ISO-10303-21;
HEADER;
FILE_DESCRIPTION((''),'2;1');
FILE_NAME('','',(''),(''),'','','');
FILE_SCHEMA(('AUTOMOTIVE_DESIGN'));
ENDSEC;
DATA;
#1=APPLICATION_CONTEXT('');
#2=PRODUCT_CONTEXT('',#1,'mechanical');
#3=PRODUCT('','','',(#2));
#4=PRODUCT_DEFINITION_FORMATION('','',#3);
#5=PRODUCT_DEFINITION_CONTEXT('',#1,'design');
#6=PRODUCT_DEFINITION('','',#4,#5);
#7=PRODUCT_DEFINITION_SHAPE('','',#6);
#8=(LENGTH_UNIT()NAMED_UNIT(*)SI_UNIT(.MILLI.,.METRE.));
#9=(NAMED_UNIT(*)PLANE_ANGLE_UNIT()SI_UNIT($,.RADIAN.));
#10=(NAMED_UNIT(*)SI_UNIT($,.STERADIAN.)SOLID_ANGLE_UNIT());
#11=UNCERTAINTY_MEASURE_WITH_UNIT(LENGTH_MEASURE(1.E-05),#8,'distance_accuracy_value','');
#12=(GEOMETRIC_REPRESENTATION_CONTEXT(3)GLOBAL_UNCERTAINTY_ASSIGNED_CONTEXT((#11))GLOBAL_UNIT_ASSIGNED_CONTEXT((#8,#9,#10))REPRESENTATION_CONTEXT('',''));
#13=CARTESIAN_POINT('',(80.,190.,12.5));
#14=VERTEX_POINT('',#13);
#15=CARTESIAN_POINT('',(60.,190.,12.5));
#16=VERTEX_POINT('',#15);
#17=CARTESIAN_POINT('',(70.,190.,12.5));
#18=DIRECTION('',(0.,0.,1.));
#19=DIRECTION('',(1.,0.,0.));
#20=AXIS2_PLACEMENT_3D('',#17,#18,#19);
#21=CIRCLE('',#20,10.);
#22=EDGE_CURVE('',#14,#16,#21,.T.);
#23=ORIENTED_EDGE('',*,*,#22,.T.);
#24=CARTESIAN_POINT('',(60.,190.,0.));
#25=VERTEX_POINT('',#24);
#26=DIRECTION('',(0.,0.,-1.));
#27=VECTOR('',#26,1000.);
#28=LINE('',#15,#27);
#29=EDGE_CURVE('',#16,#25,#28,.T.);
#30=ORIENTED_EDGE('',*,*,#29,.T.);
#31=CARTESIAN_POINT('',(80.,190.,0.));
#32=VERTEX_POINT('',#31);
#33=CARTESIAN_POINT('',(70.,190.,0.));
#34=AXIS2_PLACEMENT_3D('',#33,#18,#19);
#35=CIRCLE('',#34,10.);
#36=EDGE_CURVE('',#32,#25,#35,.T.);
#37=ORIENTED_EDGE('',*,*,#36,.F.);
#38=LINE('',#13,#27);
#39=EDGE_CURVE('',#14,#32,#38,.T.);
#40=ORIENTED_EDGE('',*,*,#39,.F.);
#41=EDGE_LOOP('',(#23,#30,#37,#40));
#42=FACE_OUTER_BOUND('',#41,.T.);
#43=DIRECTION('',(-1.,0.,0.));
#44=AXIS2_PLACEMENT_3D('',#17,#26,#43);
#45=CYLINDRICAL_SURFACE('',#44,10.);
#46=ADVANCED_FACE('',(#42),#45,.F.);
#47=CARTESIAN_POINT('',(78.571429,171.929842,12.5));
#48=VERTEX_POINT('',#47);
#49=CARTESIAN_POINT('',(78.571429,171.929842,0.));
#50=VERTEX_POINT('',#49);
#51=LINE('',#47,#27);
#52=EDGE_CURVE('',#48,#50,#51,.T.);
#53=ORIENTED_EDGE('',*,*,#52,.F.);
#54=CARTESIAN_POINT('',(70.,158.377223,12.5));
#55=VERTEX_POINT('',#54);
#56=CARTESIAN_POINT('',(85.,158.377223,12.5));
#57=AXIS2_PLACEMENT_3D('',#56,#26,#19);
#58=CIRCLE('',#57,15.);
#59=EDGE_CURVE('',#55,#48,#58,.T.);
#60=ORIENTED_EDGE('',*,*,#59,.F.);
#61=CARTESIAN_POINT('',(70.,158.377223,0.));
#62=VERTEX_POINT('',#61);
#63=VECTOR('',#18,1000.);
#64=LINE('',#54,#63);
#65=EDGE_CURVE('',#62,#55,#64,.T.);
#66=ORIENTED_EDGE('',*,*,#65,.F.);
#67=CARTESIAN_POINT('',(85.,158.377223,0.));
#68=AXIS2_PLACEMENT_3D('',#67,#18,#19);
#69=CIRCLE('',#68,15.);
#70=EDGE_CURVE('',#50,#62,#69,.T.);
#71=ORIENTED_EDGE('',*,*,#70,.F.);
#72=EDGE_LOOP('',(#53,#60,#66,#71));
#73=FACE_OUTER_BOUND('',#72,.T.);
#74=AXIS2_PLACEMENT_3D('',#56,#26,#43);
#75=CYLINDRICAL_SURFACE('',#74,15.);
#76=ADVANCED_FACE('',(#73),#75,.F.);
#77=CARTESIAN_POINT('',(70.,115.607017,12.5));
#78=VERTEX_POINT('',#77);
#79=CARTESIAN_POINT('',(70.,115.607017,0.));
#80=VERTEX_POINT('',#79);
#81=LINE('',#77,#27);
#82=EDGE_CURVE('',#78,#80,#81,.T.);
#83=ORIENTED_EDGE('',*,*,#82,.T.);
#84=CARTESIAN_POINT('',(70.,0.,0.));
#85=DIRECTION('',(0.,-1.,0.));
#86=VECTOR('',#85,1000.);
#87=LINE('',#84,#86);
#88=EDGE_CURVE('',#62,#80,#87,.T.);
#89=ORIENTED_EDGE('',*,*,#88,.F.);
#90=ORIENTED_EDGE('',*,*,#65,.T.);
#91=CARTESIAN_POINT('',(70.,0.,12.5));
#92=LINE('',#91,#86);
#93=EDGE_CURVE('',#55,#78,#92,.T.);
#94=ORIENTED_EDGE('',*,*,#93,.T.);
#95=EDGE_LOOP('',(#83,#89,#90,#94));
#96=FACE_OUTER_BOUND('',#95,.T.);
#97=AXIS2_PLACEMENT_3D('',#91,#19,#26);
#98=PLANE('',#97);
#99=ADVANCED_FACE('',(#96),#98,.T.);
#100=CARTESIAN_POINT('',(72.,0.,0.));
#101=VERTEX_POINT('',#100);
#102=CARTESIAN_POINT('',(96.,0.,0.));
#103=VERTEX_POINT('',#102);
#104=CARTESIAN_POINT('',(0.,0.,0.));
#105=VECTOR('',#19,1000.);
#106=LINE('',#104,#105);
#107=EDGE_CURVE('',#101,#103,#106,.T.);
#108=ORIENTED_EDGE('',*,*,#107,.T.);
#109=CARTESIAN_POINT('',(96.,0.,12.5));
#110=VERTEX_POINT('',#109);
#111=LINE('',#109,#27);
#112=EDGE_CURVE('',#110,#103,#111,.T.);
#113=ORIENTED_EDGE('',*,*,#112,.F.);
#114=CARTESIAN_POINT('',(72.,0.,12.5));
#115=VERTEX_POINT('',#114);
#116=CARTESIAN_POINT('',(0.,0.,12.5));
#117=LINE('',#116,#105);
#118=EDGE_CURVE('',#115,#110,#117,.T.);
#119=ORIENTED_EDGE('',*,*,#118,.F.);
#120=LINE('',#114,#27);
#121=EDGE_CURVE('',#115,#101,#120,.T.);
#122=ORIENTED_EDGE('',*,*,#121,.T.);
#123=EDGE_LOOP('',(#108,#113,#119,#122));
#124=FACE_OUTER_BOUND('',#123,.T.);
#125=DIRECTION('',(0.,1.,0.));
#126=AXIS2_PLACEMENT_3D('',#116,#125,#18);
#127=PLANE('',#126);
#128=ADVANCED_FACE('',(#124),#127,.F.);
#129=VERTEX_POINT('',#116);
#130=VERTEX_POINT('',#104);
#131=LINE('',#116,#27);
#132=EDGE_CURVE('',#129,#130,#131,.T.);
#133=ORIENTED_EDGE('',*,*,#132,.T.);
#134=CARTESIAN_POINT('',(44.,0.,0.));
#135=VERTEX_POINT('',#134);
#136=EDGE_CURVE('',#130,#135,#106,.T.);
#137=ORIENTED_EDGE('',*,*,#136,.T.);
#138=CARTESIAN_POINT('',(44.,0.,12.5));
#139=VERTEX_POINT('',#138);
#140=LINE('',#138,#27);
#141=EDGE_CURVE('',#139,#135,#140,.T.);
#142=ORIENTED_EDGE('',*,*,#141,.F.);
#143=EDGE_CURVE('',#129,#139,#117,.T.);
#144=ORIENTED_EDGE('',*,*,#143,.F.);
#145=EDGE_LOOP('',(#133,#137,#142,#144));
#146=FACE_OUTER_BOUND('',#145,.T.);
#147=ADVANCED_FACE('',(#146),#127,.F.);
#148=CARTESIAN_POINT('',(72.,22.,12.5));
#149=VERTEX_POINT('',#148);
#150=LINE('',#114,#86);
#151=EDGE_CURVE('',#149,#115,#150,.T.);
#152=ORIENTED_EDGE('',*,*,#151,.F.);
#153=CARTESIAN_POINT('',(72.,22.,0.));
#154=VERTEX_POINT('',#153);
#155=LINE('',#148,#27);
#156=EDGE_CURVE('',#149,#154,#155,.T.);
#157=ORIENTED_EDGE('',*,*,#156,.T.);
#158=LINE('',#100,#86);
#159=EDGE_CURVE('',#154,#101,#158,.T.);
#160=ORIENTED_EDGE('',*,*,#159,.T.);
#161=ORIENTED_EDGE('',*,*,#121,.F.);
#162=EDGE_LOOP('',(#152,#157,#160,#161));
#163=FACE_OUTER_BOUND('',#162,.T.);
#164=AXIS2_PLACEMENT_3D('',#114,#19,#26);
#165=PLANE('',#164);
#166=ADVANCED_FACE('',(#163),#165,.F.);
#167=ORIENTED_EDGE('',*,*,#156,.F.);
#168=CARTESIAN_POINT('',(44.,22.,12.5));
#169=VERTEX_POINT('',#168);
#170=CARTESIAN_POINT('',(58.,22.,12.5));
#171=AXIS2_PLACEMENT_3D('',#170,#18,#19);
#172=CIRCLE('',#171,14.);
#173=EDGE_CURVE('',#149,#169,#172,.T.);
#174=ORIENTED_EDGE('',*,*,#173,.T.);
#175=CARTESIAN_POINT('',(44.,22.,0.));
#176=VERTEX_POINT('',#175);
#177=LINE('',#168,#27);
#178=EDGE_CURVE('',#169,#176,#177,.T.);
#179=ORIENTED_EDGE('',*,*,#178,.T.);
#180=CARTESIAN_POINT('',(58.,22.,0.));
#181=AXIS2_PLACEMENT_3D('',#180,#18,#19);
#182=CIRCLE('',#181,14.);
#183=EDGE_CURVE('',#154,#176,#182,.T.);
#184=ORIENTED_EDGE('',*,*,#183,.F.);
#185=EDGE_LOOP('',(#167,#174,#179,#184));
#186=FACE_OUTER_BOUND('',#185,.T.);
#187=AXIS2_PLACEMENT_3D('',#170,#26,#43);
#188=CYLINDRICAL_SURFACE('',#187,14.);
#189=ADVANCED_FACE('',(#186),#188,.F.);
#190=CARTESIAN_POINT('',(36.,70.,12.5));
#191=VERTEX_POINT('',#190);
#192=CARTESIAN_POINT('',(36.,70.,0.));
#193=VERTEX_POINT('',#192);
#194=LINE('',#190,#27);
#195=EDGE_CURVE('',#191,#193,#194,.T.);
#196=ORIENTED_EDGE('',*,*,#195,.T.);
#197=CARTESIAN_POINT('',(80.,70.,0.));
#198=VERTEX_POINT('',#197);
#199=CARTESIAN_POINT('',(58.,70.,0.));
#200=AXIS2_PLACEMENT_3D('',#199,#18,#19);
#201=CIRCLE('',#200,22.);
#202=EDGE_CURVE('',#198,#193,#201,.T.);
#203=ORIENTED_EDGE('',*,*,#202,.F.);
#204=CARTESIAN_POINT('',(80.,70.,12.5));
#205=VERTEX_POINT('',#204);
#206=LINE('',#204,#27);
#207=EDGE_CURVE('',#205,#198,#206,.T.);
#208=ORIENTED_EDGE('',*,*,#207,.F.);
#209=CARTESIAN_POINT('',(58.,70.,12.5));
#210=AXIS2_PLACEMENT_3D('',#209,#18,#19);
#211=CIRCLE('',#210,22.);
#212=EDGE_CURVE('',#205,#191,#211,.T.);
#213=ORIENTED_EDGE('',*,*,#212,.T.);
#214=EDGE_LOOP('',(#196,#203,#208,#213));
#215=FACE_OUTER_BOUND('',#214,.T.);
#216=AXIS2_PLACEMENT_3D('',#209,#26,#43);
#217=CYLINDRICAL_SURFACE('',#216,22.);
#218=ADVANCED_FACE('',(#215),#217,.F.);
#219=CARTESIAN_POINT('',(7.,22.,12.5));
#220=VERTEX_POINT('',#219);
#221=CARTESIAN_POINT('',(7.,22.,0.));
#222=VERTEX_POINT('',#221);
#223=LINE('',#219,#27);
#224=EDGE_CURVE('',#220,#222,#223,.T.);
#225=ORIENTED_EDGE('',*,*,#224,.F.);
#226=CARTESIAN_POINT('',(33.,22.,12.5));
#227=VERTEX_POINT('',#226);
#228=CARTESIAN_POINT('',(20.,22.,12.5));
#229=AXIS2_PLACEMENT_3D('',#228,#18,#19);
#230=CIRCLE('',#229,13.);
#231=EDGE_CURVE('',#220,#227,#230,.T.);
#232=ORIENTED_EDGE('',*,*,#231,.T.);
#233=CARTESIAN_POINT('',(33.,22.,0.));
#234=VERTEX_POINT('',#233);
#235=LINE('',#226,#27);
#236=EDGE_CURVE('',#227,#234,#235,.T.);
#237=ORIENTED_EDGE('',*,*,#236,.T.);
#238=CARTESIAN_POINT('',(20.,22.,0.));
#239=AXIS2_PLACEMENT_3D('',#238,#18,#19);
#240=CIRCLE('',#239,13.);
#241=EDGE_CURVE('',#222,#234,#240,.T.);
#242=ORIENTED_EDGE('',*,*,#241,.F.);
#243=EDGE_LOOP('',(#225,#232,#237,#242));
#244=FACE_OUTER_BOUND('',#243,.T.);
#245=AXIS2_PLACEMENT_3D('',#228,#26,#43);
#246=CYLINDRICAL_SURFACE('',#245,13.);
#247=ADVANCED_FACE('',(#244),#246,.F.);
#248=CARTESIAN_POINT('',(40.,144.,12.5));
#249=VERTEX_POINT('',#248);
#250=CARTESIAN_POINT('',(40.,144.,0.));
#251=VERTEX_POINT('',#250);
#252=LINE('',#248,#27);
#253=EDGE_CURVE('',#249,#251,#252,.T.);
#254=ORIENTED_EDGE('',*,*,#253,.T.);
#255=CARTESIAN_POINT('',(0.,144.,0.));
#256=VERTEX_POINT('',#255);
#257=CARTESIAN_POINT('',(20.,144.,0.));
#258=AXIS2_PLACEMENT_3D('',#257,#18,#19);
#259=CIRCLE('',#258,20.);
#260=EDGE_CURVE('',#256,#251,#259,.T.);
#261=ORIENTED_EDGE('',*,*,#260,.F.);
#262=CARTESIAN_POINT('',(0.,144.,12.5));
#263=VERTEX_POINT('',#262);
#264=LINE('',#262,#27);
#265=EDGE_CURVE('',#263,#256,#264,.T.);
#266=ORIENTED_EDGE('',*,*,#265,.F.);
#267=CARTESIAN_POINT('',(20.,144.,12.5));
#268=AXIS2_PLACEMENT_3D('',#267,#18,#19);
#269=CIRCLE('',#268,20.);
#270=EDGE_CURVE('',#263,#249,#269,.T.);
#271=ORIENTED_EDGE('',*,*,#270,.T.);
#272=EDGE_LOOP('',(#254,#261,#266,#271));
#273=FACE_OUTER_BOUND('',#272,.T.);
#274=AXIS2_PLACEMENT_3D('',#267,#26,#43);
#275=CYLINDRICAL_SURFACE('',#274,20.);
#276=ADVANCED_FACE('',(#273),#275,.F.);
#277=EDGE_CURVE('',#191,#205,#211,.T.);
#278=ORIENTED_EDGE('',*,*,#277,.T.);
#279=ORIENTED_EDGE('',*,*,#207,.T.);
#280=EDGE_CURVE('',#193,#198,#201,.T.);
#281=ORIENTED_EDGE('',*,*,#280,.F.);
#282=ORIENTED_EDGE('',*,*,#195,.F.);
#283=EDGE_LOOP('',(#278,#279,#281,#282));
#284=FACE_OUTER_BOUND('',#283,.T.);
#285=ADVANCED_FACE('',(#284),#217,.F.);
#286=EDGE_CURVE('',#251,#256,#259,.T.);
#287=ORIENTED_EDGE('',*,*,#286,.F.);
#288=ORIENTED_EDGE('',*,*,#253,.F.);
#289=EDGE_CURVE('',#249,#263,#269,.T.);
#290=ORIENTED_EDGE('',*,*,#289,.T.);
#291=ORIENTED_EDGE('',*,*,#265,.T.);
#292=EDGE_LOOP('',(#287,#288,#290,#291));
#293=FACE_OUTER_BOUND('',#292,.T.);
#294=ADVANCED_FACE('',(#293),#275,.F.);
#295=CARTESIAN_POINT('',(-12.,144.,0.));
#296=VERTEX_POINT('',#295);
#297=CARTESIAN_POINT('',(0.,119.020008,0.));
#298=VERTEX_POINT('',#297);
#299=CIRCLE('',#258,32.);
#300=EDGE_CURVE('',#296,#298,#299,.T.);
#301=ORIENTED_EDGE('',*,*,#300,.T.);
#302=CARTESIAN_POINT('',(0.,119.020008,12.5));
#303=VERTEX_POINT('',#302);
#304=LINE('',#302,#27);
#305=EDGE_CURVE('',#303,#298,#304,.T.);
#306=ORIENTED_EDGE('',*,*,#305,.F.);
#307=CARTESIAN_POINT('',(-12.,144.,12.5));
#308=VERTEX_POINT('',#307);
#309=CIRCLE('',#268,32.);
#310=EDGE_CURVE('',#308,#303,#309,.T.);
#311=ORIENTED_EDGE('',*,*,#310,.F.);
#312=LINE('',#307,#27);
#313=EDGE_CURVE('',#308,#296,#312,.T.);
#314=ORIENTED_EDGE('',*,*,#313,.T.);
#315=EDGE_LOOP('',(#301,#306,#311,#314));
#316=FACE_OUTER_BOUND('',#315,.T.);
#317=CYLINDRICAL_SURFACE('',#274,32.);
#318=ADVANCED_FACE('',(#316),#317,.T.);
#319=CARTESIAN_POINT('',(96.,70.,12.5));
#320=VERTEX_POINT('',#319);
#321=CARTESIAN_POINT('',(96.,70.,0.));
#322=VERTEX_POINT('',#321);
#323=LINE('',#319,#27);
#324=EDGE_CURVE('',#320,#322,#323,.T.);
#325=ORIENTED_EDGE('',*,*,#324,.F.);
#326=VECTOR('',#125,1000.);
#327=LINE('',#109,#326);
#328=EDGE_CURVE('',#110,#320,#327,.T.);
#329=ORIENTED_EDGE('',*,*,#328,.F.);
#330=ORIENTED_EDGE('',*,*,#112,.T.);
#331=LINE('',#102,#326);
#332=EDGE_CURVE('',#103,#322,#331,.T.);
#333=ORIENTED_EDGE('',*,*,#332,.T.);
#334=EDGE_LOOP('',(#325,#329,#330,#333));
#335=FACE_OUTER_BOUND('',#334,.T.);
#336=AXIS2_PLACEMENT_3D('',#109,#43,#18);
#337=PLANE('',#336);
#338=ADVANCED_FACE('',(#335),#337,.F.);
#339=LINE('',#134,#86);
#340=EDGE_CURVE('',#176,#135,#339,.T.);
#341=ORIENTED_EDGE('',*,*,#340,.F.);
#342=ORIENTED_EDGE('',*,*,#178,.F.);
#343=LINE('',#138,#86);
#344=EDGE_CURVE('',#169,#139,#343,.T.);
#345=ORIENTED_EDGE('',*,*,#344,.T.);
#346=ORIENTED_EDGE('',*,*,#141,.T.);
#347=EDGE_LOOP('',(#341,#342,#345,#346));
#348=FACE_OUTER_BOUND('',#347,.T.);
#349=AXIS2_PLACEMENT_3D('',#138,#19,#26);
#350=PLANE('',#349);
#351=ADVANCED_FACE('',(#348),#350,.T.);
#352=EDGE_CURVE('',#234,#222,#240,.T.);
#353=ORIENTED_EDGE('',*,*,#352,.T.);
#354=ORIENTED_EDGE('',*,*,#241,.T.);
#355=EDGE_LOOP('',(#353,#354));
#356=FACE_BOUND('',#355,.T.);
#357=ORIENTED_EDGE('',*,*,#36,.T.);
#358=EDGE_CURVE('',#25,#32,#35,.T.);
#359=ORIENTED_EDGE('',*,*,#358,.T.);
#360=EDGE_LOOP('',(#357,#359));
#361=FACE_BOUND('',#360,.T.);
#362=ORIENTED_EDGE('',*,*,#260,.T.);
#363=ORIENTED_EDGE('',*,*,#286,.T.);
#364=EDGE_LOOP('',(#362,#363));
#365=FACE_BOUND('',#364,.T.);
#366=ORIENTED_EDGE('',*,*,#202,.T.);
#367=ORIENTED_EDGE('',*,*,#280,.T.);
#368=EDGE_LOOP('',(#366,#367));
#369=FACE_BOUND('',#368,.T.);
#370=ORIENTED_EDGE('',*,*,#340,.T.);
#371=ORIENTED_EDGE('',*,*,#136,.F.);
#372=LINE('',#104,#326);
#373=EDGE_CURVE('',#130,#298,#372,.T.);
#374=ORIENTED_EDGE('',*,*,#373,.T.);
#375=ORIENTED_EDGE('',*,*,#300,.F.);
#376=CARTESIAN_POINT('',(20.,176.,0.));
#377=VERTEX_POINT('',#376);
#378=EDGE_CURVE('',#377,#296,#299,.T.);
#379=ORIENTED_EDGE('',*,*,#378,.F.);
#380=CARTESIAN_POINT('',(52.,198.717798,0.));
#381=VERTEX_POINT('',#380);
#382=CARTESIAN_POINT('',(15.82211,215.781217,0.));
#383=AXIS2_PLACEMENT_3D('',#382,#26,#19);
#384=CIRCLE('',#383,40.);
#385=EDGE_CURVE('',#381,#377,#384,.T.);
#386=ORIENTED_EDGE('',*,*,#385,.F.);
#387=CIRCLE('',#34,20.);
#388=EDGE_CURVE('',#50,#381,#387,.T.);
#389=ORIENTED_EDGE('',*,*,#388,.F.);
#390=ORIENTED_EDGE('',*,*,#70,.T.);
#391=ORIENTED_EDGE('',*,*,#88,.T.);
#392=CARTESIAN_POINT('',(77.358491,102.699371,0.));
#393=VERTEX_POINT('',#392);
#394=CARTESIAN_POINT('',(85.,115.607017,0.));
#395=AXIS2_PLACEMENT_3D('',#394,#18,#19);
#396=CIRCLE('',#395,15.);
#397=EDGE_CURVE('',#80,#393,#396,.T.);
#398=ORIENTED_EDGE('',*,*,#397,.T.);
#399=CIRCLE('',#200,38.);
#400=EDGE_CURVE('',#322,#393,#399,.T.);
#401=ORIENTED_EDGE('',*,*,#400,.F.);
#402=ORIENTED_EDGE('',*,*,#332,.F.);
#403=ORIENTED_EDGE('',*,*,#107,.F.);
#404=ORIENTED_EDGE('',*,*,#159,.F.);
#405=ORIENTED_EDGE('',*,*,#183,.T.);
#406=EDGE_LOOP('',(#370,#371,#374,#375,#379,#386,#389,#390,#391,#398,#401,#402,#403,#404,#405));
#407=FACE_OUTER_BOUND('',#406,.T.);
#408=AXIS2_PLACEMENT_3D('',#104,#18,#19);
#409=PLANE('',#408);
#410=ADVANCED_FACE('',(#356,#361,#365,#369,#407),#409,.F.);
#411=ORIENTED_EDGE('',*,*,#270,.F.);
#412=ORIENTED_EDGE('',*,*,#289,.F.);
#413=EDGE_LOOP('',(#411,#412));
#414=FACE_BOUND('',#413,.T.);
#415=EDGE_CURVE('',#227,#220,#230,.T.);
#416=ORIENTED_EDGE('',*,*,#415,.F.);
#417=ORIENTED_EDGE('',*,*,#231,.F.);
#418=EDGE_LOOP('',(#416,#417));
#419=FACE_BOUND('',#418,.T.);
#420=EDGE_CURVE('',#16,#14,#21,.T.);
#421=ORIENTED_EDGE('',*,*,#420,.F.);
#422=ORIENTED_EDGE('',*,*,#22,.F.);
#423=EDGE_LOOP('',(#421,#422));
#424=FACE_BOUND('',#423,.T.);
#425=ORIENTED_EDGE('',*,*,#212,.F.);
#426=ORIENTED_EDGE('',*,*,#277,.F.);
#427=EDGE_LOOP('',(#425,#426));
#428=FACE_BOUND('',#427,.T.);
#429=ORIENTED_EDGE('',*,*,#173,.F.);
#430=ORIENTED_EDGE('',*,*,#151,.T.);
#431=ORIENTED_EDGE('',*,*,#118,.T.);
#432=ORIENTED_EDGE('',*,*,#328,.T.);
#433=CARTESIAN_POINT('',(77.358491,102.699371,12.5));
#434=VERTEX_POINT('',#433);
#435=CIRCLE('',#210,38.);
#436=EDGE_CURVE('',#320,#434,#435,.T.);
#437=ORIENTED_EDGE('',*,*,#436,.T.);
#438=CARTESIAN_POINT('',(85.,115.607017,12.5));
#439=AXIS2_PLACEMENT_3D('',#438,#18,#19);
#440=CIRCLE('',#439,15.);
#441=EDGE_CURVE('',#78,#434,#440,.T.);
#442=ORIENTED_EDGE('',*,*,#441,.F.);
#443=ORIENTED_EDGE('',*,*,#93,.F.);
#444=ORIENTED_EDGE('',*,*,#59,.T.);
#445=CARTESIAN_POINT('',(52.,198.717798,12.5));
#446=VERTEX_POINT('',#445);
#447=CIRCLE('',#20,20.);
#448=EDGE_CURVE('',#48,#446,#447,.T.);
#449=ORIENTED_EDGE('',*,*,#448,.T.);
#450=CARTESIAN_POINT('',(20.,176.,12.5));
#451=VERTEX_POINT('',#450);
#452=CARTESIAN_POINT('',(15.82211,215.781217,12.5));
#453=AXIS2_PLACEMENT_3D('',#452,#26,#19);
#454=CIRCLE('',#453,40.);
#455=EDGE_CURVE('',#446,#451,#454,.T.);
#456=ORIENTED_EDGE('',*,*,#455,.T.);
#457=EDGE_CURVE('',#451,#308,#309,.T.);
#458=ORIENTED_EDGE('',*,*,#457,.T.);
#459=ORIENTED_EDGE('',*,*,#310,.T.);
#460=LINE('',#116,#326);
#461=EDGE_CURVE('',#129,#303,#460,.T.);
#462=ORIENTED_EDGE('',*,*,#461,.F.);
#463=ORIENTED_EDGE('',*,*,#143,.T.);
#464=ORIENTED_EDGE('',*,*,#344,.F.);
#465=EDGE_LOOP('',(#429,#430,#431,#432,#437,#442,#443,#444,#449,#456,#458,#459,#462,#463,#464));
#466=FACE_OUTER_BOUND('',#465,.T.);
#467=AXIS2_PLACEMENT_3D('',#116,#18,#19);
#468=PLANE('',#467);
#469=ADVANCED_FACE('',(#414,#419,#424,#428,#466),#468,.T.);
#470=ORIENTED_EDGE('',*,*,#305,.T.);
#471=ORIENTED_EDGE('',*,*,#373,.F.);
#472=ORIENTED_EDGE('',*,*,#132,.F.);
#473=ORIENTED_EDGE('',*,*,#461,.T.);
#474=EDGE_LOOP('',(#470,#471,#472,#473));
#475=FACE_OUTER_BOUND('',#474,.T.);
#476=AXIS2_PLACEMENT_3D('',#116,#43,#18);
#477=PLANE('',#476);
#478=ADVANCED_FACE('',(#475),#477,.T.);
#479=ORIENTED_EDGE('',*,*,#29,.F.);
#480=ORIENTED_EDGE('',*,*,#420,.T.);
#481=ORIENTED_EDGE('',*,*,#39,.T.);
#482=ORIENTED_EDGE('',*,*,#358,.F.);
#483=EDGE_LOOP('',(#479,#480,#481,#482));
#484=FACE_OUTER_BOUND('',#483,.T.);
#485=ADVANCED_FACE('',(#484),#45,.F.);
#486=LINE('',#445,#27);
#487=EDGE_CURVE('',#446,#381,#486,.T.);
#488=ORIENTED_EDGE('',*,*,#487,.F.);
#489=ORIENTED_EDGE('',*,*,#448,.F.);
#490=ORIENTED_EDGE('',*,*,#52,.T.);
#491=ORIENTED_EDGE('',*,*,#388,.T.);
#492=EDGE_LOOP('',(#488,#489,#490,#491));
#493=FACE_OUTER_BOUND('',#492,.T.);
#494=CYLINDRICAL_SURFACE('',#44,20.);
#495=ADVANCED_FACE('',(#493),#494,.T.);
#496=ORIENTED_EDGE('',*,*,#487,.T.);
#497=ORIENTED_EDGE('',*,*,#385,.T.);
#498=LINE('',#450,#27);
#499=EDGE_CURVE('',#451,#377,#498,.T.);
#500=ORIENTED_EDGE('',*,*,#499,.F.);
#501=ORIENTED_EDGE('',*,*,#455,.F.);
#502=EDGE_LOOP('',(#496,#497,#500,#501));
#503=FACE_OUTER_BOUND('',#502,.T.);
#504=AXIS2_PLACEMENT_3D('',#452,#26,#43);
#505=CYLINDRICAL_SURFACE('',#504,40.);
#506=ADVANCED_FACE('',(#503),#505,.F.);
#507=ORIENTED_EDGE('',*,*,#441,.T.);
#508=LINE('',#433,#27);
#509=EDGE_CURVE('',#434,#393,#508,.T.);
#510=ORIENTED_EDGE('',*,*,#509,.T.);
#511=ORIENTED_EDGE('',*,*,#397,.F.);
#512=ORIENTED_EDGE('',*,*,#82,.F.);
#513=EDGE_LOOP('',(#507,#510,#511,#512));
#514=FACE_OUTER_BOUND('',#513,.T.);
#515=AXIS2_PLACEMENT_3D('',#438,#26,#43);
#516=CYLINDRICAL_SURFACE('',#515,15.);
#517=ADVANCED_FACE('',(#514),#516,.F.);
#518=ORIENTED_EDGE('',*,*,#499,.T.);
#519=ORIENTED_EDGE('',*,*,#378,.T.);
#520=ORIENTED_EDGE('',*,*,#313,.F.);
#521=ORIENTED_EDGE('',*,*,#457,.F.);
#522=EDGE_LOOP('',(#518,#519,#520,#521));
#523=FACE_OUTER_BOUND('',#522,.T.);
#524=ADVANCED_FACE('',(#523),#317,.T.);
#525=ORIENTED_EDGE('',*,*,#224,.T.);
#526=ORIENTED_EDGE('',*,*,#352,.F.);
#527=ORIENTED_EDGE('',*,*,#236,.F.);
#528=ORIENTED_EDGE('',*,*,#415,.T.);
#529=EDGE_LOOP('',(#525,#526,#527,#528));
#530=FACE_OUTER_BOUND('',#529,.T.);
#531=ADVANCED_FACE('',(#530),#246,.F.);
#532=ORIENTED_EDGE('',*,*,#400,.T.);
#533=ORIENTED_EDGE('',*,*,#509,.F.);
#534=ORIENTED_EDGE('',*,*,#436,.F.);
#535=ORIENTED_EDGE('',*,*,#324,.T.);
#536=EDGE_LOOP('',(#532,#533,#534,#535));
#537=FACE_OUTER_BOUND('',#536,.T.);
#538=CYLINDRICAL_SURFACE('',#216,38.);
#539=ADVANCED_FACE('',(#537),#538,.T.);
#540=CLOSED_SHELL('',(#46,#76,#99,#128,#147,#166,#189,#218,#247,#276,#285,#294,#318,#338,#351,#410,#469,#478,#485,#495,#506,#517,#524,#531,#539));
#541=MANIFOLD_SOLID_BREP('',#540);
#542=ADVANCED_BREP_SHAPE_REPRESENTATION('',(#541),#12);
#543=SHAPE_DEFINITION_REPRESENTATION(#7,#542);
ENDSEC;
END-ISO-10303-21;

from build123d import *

# Parameters (mm, degrees)
BRACKET_PROFILE_SKETCH_R   = 13
BRACKET_PROFILE_SKETCH_R_2 = 20
BRACKET_PROFILE_SKETCH_R_3 = 10
BRACKET_PROFILE_SKETCH_R_4 = 22
BRACKET_PLATE_12_5MM_DEPTH = 12.5
EDGE_FILLET_R15_R          = 15


with BuildPart() as part:
    # Bracket Profile Sketch → Bracket Plate 12.5mm (new body)
    with BuildSketch(Plane.XY):
        with BuildLine():
            Line((0, 119.020008006), (0, 0))
            Line((0, 0), (44, 0))
            Line((44, 0), (44, 22))
            ThreePointArc((44, 22), (58, 36), (72, 22))
            Line((72, 22), (72, 0))
            Line((72, 0), (96, 0))
            Line((96, 0), (96, 70))
            ThreePointArc((96, 70), (91.01229045, 88.819901149), (77.358490566, 102.699370682))
            ThreePointArc((77.358490566, 102.699370682), (71.968832717, 108.178108656), (70, 115.607017004))
            Line((70, 115.607017004), (70, 170))
            ThreePointArc((70, 170), (86.946326412, 200.621771092), (52, 198.717797887))
            ThreePointArc((52, 198.717797887), (38.977494473, 183.164838251), (20, 176))
            ThreePointArc((20, 176), (-10.194037026, 154.598119083), (0, 119.020008006))
        make_face()
        with Locations((20, 22)):
            Circle(BRACKET_PROFILE_SKETCH_R, mode=Mode.SUBTRACT)
        with Locations((20, 144)):
            Circle(BRACKET_PROFILE_SKETCH_R_2, mode=Mode.SUBTRACT)
        with Locations((70, 190)):
            Circle(BRACKET_PROFILE_SKETCH_R_3, mode=Mode.SUBTRACT)
        with Locations((58, 70)):
            Circle(BRACKET_PROFILE_SKETCH_R_4, mode=Mode.SUBTRACT)
    extrude(amount=BRACKET_PLATE_12_5MM_DEPTH)

    # Edge Fillet R15
    edge_fillet_r15_edges = [part.edges().sort_by_distance(p)[0] for p in [
        (70, 170, 6.25),
    ]]
    fillet(edge_fillet_r15_edges, radius=EDGE_FILLET_R15_R)


solid = part.part
